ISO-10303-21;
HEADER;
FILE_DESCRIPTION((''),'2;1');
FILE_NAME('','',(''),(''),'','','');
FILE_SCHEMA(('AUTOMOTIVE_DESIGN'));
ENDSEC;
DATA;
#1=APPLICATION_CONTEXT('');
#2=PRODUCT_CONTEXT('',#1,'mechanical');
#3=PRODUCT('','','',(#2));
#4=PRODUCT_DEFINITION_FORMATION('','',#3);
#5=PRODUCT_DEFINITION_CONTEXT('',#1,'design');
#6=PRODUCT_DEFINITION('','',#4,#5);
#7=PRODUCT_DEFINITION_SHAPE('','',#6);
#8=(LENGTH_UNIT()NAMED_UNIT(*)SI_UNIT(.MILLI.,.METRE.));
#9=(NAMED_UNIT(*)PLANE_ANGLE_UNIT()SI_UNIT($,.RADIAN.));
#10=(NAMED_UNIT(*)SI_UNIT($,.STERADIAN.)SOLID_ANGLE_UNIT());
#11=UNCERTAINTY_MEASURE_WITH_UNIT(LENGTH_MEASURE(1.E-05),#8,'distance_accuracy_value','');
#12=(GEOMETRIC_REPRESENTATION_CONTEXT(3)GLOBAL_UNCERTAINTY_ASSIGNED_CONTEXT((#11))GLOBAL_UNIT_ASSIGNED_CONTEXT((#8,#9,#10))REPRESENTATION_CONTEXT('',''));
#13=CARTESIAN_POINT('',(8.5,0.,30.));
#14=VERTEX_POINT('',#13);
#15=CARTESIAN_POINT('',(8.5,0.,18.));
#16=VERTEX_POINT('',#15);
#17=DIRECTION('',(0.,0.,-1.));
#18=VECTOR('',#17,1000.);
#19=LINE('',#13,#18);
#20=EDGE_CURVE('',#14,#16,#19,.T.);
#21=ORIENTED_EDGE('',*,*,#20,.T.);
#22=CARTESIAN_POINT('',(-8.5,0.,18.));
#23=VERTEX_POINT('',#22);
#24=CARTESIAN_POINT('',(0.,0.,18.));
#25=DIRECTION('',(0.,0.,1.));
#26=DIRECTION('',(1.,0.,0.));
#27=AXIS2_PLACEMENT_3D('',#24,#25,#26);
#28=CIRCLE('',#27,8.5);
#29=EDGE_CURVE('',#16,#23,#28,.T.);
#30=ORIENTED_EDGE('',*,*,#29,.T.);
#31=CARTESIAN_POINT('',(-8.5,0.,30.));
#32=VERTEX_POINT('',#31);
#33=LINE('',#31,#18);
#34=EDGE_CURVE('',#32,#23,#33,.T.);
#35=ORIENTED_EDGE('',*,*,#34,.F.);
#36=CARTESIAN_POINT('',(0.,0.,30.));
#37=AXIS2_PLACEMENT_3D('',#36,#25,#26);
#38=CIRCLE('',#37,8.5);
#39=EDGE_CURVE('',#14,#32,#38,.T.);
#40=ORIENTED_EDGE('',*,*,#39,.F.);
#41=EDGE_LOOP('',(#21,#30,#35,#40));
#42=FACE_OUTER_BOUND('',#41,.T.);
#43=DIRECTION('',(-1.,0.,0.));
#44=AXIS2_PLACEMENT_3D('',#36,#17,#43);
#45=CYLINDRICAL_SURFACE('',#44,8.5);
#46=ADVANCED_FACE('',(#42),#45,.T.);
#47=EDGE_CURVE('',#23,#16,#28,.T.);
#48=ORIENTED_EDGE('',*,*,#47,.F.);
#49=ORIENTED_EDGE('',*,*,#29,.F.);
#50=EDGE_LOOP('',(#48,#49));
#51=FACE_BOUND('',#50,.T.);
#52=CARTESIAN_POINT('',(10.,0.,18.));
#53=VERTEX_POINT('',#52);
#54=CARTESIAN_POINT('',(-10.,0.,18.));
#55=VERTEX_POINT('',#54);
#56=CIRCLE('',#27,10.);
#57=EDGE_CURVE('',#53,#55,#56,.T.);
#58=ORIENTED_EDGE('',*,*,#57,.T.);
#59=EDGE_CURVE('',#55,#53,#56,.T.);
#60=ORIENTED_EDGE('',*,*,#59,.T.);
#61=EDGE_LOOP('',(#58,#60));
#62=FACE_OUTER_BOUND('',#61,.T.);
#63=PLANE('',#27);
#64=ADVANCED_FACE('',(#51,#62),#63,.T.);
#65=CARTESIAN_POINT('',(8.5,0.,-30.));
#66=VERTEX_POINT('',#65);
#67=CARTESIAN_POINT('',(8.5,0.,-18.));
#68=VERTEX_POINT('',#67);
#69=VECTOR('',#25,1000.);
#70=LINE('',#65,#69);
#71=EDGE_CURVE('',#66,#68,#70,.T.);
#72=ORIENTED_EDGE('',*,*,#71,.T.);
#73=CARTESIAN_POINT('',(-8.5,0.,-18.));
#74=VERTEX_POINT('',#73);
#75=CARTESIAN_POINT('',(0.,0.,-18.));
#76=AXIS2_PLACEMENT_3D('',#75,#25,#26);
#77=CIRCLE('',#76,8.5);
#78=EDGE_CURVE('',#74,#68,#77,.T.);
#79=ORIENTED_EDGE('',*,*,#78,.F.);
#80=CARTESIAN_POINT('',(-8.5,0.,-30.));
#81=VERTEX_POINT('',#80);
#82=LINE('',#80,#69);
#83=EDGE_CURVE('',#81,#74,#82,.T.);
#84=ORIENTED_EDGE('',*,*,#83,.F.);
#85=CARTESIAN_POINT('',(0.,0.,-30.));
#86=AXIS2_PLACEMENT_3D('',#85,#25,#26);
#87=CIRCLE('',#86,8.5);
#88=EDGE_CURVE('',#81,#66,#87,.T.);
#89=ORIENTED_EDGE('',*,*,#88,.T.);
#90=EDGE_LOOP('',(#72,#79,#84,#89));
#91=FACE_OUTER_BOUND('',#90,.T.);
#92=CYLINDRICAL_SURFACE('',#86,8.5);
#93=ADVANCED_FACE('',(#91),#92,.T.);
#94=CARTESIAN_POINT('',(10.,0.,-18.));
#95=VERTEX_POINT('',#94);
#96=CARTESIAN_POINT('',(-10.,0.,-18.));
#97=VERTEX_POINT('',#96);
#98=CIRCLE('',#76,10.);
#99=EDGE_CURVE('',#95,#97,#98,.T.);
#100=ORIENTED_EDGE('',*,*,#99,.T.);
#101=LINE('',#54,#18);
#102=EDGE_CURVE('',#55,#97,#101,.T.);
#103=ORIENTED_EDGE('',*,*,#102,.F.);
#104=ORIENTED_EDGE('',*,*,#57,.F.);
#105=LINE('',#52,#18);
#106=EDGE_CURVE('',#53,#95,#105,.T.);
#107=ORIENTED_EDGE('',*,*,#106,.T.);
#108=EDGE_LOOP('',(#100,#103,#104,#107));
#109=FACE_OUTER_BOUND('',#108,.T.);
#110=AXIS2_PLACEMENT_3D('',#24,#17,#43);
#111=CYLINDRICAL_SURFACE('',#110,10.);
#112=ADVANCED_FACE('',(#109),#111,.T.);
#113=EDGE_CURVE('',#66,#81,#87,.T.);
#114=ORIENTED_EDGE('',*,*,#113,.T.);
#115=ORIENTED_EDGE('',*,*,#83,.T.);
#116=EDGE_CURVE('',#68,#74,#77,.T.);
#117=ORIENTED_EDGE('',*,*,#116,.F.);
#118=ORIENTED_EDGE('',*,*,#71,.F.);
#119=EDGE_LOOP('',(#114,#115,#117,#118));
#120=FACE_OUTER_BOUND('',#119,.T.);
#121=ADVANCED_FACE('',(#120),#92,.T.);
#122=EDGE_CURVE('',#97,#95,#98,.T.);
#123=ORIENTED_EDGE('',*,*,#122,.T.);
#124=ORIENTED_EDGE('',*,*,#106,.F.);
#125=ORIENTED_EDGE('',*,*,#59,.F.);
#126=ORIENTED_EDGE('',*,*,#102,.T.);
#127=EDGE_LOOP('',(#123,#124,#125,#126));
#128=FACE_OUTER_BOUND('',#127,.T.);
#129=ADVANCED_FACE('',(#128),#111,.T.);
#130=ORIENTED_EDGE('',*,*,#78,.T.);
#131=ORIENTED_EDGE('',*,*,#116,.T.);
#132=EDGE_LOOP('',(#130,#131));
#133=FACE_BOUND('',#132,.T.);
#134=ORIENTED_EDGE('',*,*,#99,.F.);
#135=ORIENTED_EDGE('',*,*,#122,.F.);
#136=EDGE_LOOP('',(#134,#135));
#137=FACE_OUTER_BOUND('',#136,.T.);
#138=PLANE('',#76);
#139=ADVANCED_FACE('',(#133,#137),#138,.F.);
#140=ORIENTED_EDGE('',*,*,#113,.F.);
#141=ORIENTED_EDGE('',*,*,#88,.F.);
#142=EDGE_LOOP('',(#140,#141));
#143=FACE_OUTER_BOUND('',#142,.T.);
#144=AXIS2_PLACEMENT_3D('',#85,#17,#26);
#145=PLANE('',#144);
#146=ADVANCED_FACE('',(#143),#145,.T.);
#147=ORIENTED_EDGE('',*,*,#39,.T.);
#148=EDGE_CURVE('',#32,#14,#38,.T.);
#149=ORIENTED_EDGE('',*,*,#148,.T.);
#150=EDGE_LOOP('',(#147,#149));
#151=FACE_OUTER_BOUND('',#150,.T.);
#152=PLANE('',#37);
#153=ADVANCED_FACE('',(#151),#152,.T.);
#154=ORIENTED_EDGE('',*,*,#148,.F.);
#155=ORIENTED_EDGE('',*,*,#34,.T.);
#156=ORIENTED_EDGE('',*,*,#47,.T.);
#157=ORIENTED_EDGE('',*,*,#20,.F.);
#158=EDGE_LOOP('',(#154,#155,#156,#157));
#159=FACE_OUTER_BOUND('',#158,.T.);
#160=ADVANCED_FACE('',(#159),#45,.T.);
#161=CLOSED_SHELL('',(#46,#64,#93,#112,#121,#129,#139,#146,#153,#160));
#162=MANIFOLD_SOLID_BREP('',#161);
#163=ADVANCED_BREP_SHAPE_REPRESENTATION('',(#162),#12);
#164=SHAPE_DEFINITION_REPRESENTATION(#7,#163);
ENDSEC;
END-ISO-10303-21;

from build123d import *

# Parameters (mm, degrees)
SKETCH_1_R      = 10
EXTRUDE_1_DEPTH = 18
SKETCH_2_R      = 8.5
EXTRUDE_2_DEPTH = 12


with BuildPart() as part:
    # 草图1 → 凸台-拉伸1 (new, symmetric)
    with BuildSketch(Plane.XY):
        Circle(SKETCH_1_R)
    extrude(amount=EXTRUDE_1_DEPTH, both=True)

    # 草图2 → 凸台-拉伸2 (add)
    with BuildSketch(Plane.XY.offset(18)):
        Circle(SKETCH_2_R)
    extrude_2 = extrude(amount=EXTRUDE_2_DEPTH)

    # 镜向1: 凸台-拉伸2 across plane
    add(extrude_2.mirror(Plane.XY))


solid = part.part
